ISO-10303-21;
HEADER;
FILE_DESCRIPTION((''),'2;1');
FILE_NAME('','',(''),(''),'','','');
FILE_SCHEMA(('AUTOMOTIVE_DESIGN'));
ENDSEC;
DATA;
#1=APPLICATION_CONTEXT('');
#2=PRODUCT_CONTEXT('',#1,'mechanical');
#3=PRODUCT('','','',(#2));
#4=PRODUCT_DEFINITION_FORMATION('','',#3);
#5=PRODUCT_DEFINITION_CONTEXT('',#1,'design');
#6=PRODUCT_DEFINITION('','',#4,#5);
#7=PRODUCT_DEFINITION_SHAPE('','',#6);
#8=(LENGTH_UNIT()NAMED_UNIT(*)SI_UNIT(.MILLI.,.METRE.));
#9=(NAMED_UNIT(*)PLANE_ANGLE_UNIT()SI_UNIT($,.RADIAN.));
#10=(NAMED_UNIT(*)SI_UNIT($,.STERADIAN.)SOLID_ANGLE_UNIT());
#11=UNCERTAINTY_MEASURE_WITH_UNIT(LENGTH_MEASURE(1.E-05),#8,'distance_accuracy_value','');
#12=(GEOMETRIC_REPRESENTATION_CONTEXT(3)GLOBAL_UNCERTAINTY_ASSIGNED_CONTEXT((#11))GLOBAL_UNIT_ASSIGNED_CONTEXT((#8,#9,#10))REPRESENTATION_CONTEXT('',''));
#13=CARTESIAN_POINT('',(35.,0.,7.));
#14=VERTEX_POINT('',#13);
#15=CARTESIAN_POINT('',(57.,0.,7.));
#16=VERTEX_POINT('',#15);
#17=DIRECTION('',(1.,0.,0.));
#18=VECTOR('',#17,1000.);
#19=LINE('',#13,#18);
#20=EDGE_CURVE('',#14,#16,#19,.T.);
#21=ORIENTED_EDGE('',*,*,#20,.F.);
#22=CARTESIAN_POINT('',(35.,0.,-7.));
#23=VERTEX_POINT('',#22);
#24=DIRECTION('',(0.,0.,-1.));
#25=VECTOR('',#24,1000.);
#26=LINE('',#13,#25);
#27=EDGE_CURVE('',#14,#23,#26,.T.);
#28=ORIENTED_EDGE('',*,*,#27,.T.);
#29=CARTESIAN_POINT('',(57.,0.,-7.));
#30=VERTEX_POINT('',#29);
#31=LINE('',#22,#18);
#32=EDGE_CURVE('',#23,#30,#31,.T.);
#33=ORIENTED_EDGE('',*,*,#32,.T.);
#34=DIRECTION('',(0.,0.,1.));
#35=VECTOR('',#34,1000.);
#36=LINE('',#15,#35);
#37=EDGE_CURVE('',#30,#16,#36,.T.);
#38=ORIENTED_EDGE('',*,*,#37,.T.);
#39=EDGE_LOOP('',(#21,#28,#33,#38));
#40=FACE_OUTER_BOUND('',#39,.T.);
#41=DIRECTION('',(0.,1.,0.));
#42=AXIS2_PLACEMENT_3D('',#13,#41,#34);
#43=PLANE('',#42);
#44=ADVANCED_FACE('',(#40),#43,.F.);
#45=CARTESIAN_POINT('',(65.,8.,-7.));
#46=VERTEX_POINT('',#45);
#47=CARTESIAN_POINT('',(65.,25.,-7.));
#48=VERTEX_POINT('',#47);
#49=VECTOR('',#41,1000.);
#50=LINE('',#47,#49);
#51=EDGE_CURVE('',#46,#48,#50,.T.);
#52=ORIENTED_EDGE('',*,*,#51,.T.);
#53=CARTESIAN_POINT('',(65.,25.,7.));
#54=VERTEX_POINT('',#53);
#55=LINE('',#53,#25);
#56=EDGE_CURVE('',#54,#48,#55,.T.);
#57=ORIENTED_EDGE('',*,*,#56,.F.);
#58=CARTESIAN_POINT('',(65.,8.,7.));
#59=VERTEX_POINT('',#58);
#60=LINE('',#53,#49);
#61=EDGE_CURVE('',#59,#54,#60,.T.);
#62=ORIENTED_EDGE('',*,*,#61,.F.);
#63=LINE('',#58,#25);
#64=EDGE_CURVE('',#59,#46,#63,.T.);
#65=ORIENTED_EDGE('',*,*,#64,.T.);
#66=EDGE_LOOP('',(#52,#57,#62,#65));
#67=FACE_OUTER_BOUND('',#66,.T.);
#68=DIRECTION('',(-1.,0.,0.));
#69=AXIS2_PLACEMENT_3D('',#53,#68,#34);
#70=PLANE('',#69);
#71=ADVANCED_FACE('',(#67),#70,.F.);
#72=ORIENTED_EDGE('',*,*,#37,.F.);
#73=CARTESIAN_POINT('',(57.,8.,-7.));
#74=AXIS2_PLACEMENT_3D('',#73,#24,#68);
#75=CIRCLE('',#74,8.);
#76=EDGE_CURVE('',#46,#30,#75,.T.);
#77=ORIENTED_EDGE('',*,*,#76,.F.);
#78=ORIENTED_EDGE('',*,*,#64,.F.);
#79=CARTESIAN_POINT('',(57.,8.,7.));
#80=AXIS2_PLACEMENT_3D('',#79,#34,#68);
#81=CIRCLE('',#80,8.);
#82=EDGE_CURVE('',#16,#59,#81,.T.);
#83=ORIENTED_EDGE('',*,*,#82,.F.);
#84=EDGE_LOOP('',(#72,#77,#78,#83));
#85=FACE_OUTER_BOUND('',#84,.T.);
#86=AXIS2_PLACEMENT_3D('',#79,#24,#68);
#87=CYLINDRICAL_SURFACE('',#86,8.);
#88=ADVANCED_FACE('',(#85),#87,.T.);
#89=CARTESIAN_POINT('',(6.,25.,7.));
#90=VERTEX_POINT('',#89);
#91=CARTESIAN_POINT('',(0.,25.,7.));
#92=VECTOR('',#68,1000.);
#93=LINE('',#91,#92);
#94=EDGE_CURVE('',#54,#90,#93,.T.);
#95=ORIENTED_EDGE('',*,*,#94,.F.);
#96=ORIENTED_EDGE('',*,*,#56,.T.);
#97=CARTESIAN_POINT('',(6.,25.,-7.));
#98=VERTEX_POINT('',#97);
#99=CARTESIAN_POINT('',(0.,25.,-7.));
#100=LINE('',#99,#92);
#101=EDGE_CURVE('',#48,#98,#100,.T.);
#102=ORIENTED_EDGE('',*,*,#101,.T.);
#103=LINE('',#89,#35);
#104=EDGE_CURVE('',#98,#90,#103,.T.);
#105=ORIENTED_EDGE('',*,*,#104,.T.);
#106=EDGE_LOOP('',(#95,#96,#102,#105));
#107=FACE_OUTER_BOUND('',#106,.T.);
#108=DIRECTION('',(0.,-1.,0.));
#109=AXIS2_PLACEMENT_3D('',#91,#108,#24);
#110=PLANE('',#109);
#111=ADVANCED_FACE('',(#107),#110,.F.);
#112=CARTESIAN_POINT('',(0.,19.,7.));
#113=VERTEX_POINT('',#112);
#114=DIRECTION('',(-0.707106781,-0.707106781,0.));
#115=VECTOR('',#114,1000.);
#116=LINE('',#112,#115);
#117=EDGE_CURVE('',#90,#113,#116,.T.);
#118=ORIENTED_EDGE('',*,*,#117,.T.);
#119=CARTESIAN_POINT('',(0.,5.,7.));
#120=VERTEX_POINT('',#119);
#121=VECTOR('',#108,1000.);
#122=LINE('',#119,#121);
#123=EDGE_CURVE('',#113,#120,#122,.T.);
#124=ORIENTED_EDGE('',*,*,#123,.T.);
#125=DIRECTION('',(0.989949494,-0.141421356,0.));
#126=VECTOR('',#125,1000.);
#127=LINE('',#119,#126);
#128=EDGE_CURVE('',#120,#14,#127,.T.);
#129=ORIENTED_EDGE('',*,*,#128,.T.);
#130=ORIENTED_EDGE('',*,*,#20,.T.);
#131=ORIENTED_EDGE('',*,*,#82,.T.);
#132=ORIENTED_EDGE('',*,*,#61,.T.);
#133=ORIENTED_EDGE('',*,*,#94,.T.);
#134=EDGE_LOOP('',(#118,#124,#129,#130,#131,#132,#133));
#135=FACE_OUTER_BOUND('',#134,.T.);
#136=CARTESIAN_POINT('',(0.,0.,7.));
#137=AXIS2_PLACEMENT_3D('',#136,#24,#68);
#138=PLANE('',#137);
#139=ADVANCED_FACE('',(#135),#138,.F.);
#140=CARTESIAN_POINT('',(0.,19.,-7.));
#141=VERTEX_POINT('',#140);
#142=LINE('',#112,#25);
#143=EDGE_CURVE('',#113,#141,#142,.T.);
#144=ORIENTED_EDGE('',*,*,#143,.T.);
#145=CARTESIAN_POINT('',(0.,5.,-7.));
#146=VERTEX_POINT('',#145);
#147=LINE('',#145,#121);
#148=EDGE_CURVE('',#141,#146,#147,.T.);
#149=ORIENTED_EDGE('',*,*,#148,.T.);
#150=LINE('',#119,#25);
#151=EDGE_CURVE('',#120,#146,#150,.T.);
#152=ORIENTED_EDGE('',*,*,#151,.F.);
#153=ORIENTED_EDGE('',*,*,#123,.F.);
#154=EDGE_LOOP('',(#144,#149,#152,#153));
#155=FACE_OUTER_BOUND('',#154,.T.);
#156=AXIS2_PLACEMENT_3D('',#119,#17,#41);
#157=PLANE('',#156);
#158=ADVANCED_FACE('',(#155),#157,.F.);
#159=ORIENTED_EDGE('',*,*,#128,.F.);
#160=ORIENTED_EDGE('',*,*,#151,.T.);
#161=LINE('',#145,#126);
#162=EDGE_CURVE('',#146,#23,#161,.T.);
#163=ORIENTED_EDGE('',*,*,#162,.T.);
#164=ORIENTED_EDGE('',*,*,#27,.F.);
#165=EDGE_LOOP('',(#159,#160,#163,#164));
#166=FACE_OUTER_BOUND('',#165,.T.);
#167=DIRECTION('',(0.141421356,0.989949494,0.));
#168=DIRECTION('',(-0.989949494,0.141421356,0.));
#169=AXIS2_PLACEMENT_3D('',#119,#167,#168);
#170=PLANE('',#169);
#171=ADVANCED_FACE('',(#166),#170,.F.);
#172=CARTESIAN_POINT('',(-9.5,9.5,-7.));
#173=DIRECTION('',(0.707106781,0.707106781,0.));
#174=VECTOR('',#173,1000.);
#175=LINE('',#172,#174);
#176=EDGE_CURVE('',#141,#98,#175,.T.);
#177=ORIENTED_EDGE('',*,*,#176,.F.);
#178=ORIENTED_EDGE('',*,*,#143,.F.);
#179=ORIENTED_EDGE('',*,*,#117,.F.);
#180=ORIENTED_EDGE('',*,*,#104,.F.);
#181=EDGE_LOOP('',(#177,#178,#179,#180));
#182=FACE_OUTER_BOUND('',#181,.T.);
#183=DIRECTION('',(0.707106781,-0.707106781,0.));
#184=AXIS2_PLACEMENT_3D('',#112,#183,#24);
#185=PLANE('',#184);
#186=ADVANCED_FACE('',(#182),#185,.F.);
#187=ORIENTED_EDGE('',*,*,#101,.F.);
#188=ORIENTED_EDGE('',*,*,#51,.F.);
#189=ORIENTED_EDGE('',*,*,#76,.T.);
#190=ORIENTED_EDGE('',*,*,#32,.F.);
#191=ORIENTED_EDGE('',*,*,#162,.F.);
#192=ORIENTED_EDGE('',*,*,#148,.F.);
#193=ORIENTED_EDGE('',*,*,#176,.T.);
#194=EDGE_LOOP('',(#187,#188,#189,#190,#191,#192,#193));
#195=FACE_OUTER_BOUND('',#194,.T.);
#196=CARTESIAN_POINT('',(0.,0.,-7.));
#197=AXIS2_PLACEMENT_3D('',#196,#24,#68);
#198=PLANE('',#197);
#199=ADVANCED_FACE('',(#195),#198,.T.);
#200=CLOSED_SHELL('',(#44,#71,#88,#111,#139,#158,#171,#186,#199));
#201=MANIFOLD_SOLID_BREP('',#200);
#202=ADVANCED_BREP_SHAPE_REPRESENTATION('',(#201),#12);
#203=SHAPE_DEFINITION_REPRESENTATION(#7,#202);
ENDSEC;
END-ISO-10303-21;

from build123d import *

# Parameters (mm, degrees)
EXTRUDE_1_DEPTH = 7
CHAMFER_1_SIZE  = 6
FILLET_1_R      = 8


with BuildPart() as part:
    # 草图1 → 凸台-拉伸1 (new, symmetric)
    with BuildSketch(Plane.XY):
        Polygon((0, 5), (0, 25), (65, 25), (65, 0), (35, 0), align=None)
    extrude(amount=EXTRUDE_1_DEPTH, both=True)

    # 倒角1
    chamfer_1_edges = [part.edges().sort_by_distance(p)[0] for p in [
        (0, 25, 0),
    ]]
    chamfer(chamfer_1_edges, length=CHAMFER_1_SIZE)

    # 圆角1
    fillet_1_edges = [part.edges().sort_by_distance(p)[0] for p in [
        (65, 0, 0),
    ]]
    fillet(fillet_1_edges, radius=FILLET_1_R)


solid = part.part
